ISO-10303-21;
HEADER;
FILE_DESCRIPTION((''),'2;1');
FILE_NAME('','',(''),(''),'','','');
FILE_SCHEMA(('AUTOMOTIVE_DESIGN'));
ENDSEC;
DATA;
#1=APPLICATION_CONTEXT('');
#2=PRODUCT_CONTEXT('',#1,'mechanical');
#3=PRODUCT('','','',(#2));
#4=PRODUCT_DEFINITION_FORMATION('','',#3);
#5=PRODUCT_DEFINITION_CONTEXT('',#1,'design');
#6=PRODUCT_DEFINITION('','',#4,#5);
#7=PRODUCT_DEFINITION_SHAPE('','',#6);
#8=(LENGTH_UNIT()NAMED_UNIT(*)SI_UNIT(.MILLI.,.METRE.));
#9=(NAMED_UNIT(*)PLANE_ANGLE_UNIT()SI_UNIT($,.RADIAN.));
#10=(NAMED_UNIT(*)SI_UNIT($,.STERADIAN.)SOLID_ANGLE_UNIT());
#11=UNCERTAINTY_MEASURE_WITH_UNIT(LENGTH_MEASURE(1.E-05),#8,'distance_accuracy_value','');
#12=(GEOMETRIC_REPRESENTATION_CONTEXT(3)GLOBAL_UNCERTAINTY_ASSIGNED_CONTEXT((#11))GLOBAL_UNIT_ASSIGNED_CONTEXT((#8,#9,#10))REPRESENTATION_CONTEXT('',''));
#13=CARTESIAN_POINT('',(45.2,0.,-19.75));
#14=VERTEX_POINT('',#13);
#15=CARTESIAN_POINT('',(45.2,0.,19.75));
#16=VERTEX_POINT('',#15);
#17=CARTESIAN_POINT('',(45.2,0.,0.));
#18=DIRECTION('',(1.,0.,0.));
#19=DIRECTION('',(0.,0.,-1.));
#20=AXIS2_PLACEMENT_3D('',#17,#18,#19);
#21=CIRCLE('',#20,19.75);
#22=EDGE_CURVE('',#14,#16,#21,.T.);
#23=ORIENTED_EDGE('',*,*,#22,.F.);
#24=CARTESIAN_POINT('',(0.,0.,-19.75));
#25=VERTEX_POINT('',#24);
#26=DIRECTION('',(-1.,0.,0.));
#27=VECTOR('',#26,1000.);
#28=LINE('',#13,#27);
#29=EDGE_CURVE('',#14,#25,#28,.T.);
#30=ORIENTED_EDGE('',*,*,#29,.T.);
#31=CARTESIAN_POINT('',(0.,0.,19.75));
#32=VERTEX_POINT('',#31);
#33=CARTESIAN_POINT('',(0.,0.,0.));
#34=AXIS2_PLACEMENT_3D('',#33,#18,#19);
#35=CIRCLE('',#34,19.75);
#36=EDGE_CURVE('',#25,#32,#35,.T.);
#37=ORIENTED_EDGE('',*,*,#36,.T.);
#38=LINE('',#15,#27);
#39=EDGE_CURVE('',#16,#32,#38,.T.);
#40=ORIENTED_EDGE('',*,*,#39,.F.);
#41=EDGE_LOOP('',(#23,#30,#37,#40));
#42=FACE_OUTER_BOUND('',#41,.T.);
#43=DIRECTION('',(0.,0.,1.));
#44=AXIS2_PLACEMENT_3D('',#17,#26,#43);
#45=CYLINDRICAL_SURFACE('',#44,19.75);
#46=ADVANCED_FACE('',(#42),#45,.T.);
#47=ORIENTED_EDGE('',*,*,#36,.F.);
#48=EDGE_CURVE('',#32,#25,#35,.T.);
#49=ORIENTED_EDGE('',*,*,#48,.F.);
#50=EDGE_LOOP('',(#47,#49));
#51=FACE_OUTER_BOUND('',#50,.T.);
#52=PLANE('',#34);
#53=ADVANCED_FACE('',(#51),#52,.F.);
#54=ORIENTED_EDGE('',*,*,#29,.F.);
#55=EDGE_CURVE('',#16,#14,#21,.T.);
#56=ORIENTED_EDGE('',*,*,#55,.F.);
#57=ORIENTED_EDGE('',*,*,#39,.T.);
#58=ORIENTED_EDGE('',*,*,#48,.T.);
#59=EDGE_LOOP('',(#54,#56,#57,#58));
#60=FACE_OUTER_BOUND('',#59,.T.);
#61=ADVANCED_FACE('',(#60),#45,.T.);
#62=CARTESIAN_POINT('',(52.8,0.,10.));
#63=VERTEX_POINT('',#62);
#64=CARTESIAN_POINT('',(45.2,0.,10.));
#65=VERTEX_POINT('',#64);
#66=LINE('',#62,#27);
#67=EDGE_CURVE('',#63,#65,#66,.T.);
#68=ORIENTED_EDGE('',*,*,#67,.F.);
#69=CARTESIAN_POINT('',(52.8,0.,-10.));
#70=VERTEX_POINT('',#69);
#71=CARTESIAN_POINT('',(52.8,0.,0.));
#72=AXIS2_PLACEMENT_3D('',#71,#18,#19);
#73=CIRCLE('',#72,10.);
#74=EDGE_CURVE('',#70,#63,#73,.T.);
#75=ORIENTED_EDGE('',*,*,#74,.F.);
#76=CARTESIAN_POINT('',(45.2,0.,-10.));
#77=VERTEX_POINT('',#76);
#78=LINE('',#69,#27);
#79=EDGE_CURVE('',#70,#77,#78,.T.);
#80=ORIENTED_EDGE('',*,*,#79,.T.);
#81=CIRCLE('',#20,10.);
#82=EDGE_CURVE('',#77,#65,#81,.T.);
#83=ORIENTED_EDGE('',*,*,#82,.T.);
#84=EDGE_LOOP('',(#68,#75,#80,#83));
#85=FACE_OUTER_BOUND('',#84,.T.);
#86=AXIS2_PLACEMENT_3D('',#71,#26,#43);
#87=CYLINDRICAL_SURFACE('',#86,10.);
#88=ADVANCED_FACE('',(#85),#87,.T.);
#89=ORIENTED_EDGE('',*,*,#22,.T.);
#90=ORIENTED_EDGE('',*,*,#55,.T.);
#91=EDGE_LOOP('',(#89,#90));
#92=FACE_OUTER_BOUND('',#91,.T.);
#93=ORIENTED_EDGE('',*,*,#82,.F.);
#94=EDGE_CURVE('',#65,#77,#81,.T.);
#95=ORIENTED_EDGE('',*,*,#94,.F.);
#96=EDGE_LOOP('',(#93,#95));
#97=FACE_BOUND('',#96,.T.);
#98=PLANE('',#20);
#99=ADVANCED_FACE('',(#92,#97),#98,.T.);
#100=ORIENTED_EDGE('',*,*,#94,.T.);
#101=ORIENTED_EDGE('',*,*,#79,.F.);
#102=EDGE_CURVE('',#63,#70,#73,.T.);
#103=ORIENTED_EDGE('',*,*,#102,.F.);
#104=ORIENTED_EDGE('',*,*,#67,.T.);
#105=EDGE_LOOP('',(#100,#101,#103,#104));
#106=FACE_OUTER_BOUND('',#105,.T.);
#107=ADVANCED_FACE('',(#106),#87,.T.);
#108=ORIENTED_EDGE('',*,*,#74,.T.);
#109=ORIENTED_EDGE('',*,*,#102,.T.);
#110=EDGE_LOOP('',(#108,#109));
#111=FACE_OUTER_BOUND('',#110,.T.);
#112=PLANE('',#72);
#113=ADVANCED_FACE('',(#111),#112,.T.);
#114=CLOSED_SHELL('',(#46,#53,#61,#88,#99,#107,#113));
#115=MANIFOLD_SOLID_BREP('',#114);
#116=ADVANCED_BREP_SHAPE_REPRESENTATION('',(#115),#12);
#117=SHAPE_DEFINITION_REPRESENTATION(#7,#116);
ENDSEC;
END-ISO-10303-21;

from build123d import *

# Parameters (mm, degrees)
SKETCH_1_R      = 19.75
EXTRUDE_1_DEPTH = 45.2
SKETCH_2_R      = 10
EXTRUDE_2_DEPTH = 7.6


with BuildPart() as part:
    # 草图1 → 凸台-拉伸1 (new body)
    with BuildSketch(Plane(origin=(0, 0, 0), x_dir=(0, 0, -1), z_dir=(1, 0, 0))):
        Circle(SKETCH_1_R)
    extrude(amount=EXTRUDE_1_DEPTH)

    # 草图2 → 凸台-拉伸2 (add)
    with BuildSketch(Plane(origin=(45.2, 0, 0), x_dir=(0, 0, -1), z_dir=(1, 0, 0))):
        with Locations(Location((0, 0, 0), (0, 0, 180))):
            Circle(SKETCH_2_R)
    extrude(amount=EXTRUDE_2_DEPTH)


solid = part.part
